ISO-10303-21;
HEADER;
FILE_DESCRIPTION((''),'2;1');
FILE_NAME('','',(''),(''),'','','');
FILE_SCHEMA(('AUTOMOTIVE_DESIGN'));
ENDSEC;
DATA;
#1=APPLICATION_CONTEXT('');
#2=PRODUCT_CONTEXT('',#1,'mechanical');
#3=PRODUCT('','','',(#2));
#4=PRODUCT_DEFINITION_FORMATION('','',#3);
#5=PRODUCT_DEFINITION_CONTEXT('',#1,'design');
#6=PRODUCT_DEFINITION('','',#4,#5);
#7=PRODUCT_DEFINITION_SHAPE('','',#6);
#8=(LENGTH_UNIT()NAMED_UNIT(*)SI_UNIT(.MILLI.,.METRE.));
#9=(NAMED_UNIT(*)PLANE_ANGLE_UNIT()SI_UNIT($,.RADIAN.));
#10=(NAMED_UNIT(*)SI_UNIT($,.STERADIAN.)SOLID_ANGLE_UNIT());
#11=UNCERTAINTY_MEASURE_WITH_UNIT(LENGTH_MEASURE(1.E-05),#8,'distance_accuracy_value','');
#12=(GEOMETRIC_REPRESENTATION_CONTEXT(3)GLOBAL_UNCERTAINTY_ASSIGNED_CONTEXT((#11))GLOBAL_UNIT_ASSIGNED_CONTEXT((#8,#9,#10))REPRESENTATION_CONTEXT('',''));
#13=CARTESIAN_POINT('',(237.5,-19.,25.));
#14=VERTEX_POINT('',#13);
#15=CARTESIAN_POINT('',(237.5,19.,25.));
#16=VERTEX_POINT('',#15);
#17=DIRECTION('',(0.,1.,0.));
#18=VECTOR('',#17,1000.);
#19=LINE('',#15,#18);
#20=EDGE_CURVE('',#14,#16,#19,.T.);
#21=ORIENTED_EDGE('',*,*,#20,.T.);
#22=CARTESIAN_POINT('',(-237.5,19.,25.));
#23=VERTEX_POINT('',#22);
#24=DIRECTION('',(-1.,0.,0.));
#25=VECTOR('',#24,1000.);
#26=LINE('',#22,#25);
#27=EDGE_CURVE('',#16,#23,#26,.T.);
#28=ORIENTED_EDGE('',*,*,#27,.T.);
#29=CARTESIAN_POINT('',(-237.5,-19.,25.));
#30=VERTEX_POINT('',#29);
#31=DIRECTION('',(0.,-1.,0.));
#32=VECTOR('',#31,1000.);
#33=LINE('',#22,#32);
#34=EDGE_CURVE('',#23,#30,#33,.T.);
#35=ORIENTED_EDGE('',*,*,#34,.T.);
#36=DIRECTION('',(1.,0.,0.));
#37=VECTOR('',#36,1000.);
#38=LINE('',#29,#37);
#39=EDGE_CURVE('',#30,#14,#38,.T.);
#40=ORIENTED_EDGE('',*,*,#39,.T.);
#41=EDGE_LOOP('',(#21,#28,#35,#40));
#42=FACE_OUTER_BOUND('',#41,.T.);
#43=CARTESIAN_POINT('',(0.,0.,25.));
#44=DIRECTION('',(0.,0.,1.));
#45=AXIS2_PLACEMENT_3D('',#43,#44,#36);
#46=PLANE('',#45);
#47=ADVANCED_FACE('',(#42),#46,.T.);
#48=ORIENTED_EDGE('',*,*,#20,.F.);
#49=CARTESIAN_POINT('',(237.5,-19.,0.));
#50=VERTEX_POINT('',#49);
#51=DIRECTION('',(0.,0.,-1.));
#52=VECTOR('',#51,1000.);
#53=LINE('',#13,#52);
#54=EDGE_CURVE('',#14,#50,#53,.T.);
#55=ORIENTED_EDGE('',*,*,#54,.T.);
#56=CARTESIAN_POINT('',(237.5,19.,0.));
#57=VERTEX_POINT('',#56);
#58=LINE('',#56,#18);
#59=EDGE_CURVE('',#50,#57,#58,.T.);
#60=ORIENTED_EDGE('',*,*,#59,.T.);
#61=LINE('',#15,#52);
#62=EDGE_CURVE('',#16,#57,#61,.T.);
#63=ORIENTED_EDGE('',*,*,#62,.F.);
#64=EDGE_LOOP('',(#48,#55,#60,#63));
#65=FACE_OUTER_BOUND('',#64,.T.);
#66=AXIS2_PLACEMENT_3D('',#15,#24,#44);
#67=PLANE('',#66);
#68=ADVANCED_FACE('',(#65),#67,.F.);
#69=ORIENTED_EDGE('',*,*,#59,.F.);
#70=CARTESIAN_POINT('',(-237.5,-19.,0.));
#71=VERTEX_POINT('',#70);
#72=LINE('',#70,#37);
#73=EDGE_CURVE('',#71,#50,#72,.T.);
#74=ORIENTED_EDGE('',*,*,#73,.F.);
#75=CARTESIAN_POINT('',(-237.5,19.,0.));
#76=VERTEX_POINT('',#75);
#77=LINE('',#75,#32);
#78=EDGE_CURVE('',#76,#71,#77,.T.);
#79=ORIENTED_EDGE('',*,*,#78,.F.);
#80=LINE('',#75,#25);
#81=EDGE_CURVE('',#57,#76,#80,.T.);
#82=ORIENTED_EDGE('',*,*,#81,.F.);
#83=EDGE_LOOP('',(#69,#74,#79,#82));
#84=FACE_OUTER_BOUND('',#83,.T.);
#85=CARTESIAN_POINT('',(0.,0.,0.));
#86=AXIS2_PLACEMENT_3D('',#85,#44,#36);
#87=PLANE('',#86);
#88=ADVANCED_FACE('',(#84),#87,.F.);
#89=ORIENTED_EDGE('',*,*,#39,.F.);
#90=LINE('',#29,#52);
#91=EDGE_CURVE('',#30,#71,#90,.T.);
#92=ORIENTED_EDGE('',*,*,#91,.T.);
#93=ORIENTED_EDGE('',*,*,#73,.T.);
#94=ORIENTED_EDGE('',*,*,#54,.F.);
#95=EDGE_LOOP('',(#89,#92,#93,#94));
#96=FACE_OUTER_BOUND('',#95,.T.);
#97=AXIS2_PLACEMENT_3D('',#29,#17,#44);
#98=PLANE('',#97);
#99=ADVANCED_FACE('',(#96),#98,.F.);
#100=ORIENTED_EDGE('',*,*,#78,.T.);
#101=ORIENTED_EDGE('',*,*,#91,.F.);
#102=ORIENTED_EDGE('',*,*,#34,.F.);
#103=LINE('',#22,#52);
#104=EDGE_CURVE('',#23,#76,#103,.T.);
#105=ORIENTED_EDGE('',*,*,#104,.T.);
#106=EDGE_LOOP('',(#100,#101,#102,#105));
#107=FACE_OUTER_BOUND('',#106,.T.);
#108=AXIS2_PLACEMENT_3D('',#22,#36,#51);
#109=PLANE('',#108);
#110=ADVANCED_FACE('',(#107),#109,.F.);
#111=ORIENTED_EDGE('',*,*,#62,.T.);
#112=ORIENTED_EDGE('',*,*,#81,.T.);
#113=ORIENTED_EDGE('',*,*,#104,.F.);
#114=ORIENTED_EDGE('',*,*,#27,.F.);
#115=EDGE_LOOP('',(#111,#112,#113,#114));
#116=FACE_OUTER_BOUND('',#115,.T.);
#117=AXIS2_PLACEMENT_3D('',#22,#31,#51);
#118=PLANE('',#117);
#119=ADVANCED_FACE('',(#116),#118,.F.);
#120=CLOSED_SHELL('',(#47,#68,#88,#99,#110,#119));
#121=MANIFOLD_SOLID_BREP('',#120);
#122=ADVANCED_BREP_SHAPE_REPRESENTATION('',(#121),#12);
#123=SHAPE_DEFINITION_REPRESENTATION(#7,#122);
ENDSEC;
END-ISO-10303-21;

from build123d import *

# Parameters (mm, degrees)
SKETCH1_W           = 475
SKETCH1_H           = 38
BOSS_EXTRUDE1_DEPTH = 25


with BuildPart() as part:
    # Sketch1 → Boss-Extrude1 (new body)
    with BuildSketch(Plane.XY):
        Rectangle(SKETCH1_W, SKETCH1_H)
    extrude(amount=BOSS_EXTRUDE1_DEPTH)


solid = part.part
